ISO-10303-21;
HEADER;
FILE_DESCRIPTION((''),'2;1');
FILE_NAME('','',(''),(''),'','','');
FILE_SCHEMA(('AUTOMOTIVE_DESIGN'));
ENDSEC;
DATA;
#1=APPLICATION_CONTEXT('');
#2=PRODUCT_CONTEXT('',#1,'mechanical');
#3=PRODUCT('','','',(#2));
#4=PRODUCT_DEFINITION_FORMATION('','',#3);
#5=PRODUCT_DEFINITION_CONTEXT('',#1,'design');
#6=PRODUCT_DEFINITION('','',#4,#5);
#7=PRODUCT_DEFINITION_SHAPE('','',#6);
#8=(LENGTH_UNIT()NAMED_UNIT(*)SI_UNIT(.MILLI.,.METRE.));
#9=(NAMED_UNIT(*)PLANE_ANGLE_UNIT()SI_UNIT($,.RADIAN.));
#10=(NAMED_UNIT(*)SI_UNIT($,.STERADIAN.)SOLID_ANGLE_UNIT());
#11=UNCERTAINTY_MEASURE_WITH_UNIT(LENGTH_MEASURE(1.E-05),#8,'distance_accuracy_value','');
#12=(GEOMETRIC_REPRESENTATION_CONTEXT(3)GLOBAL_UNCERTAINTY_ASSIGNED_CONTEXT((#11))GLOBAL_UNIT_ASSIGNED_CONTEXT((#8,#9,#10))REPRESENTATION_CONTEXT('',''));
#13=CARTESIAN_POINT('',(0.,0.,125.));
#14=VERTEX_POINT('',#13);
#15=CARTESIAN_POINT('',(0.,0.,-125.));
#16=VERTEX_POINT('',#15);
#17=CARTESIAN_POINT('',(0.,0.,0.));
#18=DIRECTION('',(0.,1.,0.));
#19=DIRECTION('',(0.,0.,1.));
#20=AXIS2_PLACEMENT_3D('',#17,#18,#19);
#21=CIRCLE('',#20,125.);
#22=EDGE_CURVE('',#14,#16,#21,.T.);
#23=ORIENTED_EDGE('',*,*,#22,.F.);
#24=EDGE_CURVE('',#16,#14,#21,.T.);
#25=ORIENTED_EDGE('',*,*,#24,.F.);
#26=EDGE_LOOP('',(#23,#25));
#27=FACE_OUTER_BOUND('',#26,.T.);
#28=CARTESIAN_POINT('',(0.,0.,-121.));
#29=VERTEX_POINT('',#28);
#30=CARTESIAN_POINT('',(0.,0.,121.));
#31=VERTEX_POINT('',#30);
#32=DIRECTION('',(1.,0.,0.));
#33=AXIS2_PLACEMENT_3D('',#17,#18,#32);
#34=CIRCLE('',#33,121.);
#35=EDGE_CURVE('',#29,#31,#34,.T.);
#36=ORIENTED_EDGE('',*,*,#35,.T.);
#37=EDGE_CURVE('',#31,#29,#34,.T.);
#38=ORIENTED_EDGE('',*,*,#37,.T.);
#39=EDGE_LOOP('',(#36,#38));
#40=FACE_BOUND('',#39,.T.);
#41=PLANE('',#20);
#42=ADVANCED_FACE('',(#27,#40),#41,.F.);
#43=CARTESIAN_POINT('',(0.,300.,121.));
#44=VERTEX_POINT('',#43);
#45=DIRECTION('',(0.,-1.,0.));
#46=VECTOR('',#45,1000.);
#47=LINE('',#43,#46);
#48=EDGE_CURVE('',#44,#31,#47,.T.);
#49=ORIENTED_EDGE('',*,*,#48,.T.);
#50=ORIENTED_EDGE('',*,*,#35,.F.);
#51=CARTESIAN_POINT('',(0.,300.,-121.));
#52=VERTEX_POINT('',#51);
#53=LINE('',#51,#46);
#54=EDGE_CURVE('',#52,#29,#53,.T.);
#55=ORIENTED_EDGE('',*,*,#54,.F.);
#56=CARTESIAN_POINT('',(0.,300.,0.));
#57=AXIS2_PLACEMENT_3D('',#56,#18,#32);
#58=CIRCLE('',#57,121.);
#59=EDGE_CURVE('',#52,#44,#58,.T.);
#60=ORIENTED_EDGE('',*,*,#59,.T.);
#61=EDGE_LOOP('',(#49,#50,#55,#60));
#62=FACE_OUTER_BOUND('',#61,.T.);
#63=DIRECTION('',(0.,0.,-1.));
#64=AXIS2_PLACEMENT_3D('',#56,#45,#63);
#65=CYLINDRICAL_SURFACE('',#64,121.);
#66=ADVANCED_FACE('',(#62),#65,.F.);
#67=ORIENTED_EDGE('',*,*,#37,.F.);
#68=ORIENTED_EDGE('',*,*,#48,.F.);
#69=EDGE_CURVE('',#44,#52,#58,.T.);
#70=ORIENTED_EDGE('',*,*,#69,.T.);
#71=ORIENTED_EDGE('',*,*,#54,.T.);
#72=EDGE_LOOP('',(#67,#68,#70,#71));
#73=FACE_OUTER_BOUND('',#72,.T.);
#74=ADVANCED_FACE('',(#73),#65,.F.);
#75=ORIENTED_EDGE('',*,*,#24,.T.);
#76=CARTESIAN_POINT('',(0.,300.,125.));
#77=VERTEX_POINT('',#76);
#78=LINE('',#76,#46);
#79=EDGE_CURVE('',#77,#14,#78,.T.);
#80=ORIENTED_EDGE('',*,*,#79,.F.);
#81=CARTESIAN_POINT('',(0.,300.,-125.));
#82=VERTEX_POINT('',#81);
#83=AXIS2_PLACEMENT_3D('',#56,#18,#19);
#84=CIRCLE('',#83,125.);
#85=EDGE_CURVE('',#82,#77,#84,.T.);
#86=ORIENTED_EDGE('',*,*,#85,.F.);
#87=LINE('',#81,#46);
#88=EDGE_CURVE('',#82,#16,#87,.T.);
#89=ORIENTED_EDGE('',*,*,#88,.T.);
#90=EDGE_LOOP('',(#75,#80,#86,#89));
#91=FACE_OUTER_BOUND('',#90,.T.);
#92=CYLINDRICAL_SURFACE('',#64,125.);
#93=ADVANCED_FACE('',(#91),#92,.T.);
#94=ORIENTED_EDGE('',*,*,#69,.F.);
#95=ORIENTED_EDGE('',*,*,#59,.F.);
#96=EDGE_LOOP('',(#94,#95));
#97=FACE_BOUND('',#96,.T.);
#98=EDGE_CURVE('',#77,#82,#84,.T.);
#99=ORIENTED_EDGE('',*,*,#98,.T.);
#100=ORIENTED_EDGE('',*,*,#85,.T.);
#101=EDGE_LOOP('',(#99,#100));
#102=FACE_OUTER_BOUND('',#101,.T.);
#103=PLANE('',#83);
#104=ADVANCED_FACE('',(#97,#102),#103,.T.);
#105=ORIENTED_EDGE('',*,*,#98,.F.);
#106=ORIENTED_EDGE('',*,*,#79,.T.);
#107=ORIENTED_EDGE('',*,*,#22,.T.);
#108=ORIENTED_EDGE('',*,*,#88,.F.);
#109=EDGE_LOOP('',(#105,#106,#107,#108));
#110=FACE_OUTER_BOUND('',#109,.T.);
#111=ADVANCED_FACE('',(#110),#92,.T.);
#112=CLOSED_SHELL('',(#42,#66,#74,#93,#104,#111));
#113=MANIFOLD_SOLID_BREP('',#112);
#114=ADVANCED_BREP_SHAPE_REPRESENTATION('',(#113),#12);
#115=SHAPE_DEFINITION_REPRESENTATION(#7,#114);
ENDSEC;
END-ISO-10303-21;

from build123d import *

# Parameters (mm, degrees)
SKETCH_1_R      = 125
SKETCH_1_R_2    = 121
EXTRUDE_1_DEPTH = 300


with BuildPart() as part:
    # 草图1 → 拉伸-薄壁1 (new body)
    with BuildSketch(Plane(origin=(0, 0, 0), x_dir=(1, 0, 0), z_dir=(0, 1, 0))):
        Circle(SKETCH_1_R)
        Circle(SKETCH_1_R_2, mode=Mode.SUBTRACT)
    extrude(amount=EXTRUDE_1_DEPTH)


solid = part.part
